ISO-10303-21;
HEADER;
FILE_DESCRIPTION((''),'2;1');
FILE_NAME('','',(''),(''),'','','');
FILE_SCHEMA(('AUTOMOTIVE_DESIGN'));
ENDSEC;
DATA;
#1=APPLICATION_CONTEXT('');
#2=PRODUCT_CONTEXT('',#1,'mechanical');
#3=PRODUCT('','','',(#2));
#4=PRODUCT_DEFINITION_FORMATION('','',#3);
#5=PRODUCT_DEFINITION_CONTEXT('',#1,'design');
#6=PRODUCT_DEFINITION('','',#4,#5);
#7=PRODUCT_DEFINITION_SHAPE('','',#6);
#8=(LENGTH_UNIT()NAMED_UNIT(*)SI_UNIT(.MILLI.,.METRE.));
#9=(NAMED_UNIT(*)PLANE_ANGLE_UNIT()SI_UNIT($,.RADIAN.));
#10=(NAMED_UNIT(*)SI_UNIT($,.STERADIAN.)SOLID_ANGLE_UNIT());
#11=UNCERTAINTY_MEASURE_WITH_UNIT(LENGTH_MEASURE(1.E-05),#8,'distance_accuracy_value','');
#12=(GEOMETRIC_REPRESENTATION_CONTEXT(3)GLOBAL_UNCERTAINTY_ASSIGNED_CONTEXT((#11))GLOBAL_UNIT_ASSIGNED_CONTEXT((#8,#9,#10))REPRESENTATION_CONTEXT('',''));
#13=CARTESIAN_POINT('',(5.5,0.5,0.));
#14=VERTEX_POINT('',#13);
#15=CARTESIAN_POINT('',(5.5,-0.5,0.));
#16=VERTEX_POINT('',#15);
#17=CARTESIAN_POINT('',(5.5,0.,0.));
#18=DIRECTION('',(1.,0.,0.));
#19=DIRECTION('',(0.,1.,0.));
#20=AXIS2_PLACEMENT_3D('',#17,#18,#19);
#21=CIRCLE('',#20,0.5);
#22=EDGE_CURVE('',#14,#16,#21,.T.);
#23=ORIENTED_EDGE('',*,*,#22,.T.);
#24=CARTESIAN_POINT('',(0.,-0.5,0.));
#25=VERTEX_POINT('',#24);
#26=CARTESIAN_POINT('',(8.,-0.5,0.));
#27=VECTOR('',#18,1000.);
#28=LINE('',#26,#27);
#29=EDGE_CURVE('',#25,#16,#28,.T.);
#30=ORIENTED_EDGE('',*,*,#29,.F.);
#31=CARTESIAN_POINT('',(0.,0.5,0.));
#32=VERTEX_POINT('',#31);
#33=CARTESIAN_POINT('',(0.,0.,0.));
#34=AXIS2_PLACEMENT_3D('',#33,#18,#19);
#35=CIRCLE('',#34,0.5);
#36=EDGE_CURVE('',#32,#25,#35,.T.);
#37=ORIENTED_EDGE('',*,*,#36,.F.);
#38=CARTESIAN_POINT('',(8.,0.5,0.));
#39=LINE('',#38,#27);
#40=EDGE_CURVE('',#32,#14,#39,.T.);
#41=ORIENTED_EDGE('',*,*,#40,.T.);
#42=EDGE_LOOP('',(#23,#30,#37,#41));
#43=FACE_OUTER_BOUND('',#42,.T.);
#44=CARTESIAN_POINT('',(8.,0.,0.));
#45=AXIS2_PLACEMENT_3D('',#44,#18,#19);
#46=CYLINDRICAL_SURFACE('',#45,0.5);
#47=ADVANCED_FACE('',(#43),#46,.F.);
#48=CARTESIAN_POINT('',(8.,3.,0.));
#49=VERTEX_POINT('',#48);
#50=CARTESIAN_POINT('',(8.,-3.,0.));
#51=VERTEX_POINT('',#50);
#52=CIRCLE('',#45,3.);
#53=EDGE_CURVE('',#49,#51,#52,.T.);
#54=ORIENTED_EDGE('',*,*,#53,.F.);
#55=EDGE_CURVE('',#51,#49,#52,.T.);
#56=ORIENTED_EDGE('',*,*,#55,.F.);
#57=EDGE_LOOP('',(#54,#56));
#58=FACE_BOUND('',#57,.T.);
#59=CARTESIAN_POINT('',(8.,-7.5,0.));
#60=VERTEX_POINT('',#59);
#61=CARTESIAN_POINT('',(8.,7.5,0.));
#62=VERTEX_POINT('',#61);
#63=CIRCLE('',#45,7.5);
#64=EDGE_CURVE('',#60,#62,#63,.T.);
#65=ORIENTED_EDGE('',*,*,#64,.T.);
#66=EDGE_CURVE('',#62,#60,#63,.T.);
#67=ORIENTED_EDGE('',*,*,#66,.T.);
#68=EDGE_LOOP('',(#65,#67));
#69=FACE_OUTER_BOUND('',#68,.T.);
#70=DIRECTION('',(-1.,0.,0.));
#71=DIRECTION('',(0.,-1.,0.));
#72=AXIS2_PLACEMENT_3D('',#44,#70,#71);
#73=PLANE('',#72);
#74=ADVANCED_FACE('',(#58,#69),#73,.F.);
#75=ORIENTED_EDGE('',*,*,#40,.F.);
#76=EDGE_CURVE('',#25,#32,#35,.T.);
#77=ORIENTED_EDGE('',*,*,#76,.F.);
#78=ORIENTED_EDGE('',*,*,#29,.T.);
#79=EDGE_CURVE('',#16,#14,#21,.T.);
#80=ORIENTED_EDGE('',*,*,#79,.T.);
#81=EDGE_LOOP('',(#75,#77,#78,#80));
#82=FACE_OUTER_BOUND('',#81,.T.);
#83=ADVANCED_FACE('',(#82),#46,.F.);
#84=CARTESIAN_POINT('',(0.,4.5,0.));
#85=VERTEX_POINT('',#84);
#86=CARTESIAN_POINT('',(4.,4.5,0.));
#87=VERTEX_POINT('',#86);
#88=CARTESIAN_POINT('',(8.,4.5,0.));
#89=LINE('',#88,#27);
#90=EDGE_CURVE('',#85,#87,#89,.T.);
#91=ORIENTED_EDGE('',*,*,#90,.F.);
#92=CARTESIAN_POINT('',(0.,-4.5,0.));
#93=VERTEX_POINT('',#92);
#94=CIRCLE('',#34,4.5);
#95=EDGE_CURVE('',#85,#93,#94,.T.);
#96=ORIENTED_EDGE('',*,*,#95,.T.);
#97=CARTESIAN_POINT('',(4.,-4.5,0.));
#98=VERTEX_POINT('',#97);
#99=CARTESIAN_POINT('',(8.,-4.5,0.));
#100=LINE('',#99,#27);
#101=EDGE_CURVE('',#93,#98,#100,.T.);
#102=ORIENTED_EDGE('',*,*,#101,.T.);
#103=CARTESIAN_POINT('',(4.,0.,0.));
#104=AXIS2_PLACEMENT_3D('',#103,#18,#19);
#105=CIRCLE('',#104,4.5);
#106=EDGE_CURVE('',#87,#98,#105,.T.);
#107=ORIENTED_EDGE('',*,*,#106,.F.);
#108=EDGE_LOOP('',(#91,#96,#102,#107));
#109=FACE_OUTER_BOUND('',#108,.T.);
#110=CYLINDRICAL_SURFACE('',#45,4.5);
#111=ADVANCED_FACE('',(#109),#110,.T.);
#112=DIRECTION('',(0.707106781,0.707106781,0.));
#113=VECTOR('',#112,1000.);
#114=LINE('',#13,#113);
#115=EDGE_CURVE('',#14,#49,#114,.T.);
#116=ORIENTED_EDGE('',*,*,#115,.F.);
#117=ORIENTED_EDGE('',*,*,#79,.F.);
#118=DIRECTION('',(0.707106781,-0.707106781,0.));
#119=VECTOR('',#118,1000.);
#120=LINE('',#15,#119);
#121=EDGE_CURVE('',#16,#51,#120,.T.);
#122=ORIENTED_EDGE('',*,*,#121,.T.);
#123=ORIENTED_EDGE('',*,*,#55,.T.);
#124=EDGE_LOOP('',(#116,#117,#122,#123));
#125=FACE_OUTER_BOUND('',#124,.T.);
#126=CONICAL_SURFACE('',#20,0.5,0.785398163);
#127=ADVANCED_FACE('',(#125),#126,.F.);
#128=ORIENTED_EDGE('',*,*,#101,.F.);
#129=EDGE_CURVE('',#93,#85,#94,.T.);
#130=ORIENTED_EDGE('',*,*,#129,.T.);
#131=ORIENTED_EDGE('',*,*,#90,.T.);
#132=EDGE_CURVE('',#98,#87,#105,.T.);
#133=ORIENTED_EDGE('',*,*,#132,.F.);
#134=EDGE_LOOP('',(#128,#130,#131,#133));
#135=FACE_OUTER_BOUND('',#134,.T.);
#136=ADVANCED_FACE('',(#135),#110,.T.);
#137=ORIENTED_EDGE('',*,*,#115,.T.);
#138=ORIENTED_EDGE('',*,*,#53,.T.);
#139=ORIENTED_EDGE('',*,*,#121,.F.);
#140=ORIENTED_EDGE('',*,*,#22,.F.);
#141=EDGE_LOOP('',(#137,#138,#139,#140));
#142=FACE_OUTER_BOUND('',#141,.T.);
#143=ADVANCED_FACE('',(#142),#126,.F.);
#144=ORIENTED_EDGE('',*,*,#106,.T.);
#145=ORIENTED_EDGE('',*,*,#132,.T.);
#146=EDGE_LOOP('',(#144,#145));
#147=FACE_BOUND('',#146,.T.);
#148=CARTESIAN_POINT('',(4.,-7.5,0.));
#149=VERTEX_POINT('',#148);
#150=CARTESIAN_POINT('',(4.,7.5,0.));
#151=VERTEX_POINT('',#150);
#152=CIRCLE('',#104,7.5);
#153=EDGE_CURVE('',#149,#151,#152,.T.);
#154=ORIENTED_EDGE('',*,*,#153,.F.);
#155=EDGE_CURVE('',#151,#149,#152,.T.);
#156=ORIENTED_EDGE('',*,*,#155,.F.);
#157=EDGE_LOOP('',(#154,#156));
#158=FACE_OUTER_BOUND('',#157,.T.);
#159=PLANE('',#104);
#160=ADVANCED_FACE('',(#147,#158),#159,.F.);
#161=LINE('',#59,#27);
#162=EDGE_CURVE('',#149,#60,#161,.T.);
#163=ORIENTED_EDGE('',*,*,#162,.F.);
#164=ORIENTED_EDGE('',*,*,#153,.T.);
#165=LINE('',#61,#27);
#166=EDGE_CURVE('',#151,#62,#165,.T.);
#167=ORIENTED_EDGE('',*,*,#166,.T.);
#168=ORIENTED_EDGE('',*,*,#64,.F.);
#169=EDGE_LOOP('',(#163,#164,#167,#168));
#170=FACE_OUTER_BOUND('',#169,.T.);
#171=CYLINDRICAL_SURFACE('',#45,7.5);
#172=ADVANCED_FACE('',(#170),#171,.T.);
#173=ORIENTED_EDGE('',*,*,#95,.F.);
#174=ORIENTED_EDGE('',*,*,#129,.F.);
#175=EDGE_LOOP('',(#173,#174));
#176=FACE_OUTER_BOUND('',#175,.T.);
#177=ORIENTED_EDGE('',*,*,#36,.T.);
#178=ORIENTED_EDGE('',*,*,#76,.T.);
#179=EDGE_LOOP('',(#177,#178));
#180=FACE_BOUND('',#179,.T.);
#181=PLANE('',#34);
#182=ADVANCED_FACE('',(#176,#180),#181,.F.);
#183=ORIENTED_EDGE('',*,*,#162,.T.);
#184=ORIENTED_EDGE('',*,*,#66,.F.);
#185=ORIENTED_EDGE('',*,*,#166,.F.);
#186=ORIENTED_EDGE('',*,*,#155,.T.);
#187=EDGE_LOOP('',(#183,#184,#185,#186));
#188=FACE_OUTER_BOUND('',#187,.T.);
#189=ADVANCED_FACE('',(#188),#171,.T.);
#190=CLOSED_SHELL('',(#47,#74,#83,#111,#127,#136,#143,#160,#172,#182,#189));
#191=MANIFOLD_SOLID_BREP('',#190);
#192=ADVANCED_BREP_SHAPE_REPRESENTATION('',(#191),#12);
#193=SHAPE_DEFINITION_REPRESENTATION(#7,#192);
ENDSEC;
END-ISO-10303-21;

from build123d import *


with BuildPart() as part:
    # Sketch1 → Revolve1 (revolve)
    with BuildSketch(Plane.XY):
        Polygon((0, 4.5), (0, 0.5), (5.5, 0.5), (8, 3), (8, 7.5), (4, 7.5), (4, 4.5), align=None)
    revolve(axis=Axis((8, 0, 0), (-1, 0, 0)))


solid = part.part
